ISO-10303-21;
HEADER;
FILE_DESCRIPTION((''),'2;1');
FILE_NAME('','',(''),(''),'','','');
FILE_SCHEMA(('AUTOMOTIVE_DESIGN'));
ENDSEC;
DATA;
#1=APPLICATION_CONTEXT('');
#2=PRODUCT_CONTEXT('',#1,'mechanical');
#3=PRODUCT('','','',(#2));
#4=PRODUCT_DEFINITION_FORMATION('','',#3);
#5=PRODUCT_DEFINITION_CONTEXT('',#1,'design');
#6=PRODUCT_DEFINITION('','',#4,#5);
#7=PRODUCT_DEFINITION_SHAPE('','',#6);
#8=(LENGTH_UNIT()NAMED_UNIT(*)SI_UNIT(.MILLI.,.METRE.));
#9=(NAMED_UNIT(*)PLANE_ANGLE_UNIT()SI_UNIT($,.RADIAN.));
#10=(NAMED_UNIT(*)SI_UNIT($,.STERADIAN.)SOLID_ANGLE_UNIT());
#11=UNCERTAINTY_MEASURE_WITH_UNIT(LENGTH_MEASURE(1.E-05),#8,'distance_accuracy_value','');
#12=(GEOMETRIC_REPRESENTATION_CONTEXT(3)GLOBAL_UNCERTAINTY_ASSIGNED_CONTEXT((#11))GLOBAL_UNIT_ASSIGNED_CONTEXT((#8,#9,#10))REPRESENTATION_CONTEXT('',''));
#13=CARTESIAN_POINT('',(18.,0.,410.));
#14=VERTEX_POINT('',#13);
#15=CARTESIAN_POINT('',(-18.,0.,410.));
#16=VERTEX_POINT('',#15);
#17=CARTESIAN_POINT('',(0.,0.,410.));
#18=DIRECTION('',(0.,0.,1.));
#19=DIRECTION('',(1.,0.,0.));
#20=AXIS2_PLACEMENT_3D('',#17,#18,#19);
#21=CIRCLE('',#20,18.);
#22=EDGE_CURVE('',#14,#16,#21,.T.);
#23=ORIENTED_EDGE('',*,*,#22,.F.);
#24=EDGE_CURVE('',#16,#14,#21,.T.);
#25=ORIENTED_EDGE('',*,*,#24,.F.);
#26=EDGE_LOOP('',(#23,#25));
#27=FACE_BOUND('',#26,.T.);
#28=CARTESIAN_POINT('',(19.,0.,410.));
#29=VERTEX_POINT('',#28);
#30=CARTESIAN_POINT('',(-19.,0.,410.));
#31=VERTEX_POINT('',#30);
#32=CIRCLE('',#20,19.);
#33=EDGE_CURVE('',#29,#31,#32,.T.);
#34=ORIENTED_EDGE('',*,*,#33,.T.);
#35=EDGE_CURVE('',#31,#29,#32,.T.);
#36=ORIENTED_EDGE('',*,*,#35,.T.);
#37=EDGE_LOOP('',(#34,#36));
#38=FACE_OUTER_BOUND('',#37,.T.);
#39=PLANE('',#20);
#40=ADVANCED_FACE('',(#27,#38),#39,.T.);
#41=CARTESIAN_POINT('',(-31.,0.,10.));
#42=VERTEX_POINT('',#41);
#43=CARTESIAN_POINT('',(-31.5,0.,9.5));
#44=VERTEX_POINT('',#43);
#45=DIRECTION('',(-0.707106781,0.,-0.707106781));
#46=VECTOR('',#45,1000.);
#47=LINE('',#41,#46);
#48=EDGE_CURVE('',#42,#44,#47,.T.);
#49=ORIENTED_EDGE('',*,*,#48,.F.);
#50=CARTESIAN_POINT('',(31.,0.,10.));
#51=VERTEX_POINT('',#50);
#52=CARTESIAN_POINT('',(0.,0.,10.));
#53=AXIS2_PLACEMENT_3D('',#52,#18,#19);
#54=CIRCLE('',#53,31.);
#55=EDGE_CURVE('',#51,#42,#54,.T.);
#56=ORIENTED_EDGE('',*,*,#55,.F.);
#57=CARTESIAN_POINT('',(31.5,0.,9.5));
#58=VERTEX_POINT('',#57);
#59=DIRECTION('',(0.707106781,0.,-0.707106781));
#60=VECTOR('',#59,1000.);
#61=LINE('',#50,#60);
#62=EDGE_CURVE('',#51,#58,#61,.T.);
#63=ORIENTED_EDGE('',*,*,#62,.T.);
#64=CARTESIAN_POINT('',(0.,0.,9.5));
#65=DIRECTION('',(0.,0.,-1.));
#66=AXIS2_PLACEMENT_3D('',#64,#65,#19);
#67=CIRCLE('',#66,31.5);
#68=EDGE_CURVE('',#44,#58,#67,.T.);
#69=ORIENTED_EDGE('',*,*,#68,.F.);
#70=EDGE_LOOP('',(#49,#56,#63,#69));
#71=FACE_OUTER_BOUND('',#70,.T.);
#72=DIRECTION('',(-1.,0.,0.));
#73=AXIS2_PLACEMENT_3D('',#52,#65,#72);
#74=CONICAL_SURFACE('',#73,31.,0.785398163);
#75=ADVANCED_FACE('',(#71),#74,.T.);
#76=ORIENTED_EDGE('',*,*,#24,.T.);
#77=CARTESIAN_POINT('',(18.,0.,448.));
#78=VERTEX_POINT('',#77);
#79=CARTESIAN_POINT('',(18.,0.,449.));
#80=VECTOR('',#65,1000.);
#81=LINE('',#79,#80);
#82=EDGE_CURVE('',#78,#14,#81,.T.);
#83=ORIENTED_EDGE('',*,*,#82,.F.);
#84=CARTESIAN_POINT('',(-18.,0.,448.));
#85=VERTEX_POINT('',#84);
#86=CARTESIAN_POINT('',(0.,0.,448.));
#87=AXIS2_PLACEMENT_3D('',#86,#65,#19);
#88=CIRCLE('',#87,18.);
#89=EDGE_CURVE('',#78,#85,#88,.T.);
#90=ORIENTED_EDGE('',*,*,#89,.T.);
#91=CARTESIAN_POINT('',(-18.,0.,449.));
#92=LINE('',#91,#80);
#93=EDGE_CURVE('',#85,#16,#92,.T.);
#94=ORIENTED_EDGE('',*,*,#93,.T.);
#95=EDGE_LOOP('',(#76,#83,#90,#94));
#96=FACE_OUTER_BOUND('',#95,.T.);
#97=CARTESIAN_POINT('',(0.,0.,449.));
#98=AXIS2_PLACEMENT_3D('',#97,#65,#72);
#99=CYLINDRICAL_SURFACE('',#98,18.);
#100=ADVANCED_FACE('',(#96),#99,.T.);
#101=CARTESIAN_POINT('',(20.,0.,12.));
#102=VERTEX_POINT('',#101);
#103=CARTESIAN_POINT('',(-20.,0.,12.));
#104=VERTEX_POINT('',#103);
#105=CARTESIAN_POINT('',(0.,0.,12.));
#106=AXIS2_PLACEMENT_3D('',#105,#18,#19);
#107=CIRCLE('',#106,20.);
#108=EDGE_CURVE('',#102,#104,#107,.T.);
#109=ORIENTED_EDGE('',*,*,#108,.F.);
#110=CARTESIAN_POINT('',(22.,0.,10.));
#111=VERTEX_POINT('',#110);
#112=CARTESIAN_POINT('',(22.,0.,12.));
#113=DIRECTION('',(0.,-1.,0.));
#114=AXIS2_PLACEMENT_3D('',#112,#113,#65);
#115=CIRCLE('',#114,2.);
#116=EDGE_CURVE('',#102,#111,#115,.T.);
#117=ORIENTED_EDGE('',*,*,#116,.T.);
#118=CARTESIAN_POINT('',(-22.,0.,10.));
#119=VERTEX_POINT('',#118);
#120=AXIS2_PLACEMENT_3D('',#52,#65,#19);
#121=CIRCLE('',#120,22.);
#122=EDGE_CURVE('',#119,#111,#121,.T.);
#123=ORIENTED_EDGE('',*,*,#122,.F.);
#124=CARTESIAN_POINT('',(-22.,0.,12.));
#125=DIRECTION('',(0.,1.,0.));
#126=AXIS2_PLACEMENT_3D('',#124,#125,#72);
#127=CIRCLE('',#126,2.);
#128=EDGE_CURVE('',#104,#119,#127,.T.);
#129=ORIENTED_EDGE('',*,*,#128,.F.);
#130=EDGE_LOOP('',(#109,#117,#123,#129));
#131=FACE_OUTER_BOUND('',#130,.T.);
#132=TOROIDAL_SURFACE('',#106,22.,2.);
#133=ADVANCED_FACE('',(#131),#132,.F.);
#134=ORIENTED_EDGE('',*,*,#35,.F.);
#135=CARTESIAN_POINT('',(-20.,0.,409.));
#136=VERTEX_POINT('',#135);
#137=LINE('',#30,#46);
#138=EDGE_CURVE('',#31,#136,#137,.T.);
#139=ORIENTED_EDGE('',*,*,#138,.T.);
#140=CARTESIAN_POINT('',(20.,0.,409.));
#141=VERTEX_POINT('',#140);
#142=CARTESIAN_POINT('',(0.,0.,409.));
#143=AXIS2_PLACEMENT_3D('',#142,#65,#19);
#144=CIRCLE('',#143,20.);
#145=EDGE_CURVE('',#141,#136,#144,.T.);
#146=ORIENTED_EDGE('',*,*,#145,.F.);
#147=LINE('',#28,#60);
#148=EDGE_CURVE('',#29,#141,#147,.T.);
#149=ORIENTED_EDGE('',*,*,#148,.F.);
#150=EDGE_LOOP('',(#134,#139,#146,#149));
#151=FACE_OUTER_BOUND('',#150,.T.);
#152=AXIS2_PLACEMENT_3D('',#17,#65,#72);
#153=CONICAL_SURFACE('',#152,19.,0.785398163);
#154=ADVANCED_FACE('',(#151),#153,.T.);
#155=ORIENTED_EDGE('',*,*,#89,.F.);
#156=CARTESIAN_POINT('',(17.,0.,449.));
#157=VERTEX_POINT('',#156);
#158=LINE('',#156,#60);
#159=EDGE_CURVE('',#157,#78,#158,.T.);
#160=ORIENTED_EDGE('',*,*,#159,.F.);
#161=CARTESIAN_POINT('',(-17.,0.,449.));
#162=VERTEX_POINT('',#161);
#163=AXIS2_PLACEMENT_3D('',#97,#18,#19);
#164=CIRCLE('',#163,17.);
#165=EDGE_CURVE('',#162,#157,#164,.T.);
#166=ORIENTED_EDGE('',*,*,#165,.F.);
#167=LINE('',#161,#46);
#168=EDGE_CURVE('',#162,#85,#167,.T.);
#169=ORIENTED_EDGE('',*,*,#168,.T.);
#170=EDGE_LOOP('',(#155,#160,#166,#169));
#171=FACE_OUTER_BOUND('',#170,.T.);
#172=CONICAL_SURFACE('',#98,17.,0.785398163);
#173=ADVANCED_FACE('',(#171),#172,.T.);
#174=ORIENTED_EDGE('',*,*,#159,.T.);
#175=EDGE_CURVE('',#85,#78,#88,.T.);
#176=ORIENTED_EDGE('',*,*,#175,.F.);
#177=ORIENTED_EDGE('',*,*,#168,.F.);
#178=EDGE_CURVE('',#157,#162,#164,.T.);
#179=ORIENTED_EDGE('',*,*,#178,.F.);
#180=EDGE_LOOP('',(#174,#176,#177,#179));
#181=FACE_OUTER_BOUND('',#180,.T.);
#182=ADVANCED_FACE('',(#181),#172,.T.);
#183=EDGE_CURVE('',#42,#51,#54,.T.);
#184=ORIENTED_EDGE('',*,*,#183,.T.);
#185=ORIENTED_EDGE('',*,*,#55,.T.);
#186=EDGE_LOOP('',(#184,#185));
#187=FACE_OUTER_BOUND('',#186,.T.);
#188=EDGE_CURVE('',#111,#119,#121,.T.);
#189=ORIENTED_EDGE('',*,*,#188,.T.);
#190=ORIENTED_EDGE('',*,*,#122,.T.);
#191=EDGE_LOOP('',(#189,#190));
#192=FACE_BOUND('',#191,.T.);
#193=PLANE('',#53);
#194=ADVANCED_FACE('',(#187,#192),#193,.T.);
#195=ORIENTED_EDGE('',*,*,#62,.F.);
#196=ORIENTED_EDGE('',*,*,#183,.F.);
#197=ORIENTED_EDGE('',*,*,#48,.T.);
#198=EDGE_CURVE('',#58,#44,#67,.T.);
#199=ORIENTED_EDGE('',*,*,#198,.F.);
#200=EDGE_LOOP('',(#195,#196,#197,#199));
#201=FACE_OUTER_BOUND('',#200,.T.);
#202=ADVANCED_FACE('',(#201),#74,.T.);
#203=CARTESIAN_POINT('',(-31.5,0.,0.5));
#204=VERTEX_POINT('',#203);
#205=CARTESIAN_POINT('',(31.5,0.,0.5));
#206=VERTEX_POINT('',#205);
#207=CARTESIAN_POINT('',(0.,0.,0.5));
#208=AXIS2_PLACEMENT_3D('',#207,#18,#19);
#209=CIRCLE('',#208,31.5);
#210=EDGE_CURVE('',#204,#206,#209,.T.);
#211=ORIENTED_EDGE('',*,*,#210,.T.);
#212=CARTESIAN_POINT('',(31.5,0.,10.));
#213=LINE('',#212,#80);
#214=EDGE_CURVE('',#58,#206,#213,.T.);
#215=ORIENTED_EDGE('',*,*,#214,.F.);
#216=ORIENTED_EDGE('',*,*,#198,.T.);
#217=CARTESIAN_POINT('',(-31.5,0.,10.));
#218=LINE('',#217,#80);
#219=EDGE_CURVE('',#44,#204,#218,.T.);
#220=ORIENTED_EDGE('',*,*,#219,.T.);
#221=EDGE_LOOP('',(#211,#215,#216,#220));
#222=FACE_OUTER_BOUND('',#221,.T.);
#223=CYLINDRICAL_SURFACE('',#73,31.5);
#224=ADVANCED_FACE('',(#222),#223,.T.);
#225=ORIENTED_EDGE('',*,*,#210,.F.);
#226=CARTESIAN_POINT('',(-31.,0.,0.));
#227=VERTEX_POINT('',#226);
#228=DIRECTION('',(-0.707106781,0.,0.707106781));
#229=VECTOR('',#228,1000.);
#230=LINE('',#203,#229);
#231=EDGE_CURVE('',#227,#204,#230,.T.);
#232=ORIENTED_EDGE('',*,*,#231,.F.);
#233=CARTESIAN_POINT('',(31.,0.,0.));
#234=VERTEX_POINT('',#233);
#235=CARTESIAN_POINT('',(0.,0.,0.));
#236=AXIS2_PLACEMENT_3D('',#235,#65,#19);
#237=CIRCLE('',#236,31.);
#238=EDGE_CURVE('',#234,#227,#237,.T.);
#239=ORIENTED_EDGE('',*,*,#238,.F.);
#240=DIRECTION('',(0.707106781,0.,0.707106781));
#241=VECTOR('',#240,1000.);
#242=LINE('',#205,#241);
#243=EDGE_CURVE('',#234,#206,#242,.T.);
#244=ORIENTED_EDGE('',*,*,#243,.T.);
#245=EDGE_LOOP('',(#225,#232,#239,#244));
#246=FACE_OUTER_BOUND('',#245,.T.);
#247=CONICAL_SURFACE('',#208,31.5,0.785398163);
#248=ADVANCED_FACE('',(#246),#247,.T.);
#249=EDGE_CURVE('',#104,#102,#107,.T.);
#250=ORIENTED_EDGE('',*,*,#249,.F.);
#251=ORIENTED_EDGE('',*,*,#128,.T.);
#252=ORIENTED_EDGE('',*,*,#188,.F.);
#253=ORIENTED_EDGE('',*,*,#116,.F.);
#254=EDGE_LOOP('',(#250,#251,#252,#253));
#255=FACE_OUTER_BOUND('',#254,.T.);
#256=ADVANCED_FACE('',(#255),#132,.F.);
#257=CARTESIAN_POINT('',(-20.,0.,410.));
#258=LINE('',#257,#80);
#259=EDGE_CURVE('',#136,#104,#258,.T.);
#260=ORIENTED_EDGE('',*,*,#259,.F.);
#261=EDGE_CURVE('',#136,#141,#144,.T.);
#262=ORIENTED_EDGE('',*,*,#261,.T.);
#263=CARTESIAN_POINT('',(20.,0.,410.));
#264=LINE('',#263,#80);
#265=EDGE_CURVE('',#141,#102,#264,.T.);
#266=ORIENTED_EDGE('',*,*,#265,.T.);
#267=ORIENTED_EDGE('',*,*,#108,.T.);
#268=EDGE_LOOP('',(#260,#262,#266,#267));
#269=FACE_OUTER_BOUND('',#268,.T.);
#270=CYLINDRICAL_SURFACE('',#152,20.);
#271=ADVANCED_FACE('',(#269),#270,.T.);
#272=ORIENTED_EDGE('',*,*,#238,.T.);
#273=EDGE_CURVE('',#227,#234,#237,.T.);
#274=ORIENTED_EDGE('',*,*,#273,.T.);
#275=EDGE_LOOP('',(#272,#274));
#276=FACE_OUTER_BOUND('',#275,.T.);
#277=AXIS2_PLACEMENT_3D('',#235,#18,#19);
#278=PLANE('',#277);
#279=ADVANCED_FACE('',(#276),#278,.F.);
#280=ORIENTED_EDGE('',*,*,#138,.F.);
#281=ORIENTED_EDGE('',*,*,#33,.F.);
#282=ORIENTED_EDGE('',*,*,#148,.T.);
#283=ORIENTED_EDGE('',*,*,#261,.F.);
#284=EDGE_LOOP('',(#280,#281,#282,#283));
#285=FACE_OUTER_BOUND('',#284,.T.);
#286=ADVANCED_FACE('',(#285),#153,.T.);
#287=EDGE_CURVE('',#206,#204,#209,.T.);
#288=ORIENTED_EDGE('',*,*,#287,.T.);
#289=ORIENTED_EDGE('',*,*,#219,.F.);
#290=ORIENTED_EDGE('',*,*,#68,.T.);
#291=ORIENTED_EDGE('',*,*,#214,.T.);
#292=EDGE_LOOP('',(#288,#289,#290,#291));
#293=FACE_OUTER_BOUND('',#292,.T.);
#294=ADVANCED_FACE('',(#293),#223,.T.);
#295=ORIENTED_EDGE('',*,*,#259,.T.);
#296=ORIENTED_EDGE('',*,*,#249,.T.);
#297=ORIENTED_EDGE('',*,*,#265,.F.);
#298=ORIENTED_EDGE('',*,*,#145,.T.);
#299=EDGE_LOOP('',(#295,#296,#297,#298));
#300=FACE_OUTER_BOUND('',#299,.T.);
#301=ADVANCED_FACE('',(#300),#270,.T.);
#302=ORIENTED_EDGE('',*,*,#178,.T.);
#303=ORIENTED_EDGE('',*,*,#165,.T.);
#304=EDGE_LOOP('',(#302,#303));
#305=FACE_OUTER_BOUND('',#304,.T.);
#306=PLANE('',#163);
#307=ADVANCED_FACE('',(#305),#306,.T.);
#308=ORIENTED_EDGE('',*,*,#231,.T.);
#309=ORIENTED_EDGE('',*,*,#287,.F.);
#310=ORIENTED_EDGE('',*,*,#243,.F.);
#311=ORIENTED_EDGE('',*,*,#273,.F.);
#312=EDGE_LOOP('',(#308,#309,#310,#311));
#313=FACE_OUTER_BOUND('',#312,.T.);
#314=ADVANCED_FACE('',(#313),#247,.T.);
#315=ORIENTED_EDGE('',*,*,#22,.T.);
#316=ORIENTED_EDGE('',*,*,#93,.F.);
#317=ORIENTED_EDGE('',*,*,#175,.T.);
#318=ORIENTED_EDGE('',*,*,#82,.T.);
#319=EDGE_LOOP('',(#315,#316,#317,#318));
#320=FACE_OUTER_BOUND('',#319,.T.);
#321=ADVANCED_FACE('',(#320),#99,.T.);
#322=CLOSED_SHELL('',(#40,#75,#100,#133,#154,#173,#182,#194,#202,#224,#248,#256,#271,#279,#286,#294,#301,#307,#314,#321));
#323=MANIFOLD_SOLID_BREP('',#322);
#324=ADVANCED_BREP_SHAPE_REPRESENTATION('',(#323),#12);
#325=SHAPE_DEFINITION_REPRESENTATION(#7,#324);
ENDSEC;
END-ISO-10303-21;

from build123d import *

# Parameters (mm, degrees)
SKETCH_1_R      = 31.5
EXTRUDE_1_DEPTH = 10
SKETCH_2_R      = 20
EXTRUDE_2_DEPTH = 400
SKETCH_3_R      = 18
EXTRUDE_3_DEPTH = 39
FILLET_1_R      = 2
CHAMFER_2_SIZE  = 1
CHAMFER_3_SIZE  = 0.5


with BuildPart() as part:
    # 草图1 → 凸台-拉伸1 (new body)
    with BuildSketch(Plane.XY):
        Circle(SKETCH_1_R)
    extrude(amount=EXTRUDE_1_DEPTH)

    # 草图2 → 凸台-拉伸2 (add)
    with BuildSketch(Plane.XY.offset(10)):
        Circle(SKETCH_2_R)
    extrude(amount=EXTRUDE_2_DEPTH)

    # 草图3 → 凸台-拉伸3 (add)
    with BuildSketch(Plane.XY.offset(410)):
        Circle(SKETCH_3_R)
    extrude(amount=EXTRUDE_3_DEPTH)

    # 圆角1
    fillet_1_edges = [part.edges().sort_by_distance(p)[0] for p in [
        (-20, 0, 10),
    ]]
    fillet(fillet_1_edges, radius=FILLET_1_R)

    # 倒角2
    chamfer_2_edges = [part.edges().sort_by_distance(p)[0] for p in [
        (-18, 0, 449),
        (-20, 0, 410),
    ]]
    chamfer(chamfer_2_edges, length=CHAMFER_2_SIZE)

    # 倒角3
    chamfer_3_edges = [part.edges().sort_by_distance(p)[0] for p in [
        (-31.5, 0, 0),
        (-31.5, 0, 10),
    ]]
    chamfer(chamfer_3_edges, length=CHAMFER_3_SIZE)


solid = part.part
